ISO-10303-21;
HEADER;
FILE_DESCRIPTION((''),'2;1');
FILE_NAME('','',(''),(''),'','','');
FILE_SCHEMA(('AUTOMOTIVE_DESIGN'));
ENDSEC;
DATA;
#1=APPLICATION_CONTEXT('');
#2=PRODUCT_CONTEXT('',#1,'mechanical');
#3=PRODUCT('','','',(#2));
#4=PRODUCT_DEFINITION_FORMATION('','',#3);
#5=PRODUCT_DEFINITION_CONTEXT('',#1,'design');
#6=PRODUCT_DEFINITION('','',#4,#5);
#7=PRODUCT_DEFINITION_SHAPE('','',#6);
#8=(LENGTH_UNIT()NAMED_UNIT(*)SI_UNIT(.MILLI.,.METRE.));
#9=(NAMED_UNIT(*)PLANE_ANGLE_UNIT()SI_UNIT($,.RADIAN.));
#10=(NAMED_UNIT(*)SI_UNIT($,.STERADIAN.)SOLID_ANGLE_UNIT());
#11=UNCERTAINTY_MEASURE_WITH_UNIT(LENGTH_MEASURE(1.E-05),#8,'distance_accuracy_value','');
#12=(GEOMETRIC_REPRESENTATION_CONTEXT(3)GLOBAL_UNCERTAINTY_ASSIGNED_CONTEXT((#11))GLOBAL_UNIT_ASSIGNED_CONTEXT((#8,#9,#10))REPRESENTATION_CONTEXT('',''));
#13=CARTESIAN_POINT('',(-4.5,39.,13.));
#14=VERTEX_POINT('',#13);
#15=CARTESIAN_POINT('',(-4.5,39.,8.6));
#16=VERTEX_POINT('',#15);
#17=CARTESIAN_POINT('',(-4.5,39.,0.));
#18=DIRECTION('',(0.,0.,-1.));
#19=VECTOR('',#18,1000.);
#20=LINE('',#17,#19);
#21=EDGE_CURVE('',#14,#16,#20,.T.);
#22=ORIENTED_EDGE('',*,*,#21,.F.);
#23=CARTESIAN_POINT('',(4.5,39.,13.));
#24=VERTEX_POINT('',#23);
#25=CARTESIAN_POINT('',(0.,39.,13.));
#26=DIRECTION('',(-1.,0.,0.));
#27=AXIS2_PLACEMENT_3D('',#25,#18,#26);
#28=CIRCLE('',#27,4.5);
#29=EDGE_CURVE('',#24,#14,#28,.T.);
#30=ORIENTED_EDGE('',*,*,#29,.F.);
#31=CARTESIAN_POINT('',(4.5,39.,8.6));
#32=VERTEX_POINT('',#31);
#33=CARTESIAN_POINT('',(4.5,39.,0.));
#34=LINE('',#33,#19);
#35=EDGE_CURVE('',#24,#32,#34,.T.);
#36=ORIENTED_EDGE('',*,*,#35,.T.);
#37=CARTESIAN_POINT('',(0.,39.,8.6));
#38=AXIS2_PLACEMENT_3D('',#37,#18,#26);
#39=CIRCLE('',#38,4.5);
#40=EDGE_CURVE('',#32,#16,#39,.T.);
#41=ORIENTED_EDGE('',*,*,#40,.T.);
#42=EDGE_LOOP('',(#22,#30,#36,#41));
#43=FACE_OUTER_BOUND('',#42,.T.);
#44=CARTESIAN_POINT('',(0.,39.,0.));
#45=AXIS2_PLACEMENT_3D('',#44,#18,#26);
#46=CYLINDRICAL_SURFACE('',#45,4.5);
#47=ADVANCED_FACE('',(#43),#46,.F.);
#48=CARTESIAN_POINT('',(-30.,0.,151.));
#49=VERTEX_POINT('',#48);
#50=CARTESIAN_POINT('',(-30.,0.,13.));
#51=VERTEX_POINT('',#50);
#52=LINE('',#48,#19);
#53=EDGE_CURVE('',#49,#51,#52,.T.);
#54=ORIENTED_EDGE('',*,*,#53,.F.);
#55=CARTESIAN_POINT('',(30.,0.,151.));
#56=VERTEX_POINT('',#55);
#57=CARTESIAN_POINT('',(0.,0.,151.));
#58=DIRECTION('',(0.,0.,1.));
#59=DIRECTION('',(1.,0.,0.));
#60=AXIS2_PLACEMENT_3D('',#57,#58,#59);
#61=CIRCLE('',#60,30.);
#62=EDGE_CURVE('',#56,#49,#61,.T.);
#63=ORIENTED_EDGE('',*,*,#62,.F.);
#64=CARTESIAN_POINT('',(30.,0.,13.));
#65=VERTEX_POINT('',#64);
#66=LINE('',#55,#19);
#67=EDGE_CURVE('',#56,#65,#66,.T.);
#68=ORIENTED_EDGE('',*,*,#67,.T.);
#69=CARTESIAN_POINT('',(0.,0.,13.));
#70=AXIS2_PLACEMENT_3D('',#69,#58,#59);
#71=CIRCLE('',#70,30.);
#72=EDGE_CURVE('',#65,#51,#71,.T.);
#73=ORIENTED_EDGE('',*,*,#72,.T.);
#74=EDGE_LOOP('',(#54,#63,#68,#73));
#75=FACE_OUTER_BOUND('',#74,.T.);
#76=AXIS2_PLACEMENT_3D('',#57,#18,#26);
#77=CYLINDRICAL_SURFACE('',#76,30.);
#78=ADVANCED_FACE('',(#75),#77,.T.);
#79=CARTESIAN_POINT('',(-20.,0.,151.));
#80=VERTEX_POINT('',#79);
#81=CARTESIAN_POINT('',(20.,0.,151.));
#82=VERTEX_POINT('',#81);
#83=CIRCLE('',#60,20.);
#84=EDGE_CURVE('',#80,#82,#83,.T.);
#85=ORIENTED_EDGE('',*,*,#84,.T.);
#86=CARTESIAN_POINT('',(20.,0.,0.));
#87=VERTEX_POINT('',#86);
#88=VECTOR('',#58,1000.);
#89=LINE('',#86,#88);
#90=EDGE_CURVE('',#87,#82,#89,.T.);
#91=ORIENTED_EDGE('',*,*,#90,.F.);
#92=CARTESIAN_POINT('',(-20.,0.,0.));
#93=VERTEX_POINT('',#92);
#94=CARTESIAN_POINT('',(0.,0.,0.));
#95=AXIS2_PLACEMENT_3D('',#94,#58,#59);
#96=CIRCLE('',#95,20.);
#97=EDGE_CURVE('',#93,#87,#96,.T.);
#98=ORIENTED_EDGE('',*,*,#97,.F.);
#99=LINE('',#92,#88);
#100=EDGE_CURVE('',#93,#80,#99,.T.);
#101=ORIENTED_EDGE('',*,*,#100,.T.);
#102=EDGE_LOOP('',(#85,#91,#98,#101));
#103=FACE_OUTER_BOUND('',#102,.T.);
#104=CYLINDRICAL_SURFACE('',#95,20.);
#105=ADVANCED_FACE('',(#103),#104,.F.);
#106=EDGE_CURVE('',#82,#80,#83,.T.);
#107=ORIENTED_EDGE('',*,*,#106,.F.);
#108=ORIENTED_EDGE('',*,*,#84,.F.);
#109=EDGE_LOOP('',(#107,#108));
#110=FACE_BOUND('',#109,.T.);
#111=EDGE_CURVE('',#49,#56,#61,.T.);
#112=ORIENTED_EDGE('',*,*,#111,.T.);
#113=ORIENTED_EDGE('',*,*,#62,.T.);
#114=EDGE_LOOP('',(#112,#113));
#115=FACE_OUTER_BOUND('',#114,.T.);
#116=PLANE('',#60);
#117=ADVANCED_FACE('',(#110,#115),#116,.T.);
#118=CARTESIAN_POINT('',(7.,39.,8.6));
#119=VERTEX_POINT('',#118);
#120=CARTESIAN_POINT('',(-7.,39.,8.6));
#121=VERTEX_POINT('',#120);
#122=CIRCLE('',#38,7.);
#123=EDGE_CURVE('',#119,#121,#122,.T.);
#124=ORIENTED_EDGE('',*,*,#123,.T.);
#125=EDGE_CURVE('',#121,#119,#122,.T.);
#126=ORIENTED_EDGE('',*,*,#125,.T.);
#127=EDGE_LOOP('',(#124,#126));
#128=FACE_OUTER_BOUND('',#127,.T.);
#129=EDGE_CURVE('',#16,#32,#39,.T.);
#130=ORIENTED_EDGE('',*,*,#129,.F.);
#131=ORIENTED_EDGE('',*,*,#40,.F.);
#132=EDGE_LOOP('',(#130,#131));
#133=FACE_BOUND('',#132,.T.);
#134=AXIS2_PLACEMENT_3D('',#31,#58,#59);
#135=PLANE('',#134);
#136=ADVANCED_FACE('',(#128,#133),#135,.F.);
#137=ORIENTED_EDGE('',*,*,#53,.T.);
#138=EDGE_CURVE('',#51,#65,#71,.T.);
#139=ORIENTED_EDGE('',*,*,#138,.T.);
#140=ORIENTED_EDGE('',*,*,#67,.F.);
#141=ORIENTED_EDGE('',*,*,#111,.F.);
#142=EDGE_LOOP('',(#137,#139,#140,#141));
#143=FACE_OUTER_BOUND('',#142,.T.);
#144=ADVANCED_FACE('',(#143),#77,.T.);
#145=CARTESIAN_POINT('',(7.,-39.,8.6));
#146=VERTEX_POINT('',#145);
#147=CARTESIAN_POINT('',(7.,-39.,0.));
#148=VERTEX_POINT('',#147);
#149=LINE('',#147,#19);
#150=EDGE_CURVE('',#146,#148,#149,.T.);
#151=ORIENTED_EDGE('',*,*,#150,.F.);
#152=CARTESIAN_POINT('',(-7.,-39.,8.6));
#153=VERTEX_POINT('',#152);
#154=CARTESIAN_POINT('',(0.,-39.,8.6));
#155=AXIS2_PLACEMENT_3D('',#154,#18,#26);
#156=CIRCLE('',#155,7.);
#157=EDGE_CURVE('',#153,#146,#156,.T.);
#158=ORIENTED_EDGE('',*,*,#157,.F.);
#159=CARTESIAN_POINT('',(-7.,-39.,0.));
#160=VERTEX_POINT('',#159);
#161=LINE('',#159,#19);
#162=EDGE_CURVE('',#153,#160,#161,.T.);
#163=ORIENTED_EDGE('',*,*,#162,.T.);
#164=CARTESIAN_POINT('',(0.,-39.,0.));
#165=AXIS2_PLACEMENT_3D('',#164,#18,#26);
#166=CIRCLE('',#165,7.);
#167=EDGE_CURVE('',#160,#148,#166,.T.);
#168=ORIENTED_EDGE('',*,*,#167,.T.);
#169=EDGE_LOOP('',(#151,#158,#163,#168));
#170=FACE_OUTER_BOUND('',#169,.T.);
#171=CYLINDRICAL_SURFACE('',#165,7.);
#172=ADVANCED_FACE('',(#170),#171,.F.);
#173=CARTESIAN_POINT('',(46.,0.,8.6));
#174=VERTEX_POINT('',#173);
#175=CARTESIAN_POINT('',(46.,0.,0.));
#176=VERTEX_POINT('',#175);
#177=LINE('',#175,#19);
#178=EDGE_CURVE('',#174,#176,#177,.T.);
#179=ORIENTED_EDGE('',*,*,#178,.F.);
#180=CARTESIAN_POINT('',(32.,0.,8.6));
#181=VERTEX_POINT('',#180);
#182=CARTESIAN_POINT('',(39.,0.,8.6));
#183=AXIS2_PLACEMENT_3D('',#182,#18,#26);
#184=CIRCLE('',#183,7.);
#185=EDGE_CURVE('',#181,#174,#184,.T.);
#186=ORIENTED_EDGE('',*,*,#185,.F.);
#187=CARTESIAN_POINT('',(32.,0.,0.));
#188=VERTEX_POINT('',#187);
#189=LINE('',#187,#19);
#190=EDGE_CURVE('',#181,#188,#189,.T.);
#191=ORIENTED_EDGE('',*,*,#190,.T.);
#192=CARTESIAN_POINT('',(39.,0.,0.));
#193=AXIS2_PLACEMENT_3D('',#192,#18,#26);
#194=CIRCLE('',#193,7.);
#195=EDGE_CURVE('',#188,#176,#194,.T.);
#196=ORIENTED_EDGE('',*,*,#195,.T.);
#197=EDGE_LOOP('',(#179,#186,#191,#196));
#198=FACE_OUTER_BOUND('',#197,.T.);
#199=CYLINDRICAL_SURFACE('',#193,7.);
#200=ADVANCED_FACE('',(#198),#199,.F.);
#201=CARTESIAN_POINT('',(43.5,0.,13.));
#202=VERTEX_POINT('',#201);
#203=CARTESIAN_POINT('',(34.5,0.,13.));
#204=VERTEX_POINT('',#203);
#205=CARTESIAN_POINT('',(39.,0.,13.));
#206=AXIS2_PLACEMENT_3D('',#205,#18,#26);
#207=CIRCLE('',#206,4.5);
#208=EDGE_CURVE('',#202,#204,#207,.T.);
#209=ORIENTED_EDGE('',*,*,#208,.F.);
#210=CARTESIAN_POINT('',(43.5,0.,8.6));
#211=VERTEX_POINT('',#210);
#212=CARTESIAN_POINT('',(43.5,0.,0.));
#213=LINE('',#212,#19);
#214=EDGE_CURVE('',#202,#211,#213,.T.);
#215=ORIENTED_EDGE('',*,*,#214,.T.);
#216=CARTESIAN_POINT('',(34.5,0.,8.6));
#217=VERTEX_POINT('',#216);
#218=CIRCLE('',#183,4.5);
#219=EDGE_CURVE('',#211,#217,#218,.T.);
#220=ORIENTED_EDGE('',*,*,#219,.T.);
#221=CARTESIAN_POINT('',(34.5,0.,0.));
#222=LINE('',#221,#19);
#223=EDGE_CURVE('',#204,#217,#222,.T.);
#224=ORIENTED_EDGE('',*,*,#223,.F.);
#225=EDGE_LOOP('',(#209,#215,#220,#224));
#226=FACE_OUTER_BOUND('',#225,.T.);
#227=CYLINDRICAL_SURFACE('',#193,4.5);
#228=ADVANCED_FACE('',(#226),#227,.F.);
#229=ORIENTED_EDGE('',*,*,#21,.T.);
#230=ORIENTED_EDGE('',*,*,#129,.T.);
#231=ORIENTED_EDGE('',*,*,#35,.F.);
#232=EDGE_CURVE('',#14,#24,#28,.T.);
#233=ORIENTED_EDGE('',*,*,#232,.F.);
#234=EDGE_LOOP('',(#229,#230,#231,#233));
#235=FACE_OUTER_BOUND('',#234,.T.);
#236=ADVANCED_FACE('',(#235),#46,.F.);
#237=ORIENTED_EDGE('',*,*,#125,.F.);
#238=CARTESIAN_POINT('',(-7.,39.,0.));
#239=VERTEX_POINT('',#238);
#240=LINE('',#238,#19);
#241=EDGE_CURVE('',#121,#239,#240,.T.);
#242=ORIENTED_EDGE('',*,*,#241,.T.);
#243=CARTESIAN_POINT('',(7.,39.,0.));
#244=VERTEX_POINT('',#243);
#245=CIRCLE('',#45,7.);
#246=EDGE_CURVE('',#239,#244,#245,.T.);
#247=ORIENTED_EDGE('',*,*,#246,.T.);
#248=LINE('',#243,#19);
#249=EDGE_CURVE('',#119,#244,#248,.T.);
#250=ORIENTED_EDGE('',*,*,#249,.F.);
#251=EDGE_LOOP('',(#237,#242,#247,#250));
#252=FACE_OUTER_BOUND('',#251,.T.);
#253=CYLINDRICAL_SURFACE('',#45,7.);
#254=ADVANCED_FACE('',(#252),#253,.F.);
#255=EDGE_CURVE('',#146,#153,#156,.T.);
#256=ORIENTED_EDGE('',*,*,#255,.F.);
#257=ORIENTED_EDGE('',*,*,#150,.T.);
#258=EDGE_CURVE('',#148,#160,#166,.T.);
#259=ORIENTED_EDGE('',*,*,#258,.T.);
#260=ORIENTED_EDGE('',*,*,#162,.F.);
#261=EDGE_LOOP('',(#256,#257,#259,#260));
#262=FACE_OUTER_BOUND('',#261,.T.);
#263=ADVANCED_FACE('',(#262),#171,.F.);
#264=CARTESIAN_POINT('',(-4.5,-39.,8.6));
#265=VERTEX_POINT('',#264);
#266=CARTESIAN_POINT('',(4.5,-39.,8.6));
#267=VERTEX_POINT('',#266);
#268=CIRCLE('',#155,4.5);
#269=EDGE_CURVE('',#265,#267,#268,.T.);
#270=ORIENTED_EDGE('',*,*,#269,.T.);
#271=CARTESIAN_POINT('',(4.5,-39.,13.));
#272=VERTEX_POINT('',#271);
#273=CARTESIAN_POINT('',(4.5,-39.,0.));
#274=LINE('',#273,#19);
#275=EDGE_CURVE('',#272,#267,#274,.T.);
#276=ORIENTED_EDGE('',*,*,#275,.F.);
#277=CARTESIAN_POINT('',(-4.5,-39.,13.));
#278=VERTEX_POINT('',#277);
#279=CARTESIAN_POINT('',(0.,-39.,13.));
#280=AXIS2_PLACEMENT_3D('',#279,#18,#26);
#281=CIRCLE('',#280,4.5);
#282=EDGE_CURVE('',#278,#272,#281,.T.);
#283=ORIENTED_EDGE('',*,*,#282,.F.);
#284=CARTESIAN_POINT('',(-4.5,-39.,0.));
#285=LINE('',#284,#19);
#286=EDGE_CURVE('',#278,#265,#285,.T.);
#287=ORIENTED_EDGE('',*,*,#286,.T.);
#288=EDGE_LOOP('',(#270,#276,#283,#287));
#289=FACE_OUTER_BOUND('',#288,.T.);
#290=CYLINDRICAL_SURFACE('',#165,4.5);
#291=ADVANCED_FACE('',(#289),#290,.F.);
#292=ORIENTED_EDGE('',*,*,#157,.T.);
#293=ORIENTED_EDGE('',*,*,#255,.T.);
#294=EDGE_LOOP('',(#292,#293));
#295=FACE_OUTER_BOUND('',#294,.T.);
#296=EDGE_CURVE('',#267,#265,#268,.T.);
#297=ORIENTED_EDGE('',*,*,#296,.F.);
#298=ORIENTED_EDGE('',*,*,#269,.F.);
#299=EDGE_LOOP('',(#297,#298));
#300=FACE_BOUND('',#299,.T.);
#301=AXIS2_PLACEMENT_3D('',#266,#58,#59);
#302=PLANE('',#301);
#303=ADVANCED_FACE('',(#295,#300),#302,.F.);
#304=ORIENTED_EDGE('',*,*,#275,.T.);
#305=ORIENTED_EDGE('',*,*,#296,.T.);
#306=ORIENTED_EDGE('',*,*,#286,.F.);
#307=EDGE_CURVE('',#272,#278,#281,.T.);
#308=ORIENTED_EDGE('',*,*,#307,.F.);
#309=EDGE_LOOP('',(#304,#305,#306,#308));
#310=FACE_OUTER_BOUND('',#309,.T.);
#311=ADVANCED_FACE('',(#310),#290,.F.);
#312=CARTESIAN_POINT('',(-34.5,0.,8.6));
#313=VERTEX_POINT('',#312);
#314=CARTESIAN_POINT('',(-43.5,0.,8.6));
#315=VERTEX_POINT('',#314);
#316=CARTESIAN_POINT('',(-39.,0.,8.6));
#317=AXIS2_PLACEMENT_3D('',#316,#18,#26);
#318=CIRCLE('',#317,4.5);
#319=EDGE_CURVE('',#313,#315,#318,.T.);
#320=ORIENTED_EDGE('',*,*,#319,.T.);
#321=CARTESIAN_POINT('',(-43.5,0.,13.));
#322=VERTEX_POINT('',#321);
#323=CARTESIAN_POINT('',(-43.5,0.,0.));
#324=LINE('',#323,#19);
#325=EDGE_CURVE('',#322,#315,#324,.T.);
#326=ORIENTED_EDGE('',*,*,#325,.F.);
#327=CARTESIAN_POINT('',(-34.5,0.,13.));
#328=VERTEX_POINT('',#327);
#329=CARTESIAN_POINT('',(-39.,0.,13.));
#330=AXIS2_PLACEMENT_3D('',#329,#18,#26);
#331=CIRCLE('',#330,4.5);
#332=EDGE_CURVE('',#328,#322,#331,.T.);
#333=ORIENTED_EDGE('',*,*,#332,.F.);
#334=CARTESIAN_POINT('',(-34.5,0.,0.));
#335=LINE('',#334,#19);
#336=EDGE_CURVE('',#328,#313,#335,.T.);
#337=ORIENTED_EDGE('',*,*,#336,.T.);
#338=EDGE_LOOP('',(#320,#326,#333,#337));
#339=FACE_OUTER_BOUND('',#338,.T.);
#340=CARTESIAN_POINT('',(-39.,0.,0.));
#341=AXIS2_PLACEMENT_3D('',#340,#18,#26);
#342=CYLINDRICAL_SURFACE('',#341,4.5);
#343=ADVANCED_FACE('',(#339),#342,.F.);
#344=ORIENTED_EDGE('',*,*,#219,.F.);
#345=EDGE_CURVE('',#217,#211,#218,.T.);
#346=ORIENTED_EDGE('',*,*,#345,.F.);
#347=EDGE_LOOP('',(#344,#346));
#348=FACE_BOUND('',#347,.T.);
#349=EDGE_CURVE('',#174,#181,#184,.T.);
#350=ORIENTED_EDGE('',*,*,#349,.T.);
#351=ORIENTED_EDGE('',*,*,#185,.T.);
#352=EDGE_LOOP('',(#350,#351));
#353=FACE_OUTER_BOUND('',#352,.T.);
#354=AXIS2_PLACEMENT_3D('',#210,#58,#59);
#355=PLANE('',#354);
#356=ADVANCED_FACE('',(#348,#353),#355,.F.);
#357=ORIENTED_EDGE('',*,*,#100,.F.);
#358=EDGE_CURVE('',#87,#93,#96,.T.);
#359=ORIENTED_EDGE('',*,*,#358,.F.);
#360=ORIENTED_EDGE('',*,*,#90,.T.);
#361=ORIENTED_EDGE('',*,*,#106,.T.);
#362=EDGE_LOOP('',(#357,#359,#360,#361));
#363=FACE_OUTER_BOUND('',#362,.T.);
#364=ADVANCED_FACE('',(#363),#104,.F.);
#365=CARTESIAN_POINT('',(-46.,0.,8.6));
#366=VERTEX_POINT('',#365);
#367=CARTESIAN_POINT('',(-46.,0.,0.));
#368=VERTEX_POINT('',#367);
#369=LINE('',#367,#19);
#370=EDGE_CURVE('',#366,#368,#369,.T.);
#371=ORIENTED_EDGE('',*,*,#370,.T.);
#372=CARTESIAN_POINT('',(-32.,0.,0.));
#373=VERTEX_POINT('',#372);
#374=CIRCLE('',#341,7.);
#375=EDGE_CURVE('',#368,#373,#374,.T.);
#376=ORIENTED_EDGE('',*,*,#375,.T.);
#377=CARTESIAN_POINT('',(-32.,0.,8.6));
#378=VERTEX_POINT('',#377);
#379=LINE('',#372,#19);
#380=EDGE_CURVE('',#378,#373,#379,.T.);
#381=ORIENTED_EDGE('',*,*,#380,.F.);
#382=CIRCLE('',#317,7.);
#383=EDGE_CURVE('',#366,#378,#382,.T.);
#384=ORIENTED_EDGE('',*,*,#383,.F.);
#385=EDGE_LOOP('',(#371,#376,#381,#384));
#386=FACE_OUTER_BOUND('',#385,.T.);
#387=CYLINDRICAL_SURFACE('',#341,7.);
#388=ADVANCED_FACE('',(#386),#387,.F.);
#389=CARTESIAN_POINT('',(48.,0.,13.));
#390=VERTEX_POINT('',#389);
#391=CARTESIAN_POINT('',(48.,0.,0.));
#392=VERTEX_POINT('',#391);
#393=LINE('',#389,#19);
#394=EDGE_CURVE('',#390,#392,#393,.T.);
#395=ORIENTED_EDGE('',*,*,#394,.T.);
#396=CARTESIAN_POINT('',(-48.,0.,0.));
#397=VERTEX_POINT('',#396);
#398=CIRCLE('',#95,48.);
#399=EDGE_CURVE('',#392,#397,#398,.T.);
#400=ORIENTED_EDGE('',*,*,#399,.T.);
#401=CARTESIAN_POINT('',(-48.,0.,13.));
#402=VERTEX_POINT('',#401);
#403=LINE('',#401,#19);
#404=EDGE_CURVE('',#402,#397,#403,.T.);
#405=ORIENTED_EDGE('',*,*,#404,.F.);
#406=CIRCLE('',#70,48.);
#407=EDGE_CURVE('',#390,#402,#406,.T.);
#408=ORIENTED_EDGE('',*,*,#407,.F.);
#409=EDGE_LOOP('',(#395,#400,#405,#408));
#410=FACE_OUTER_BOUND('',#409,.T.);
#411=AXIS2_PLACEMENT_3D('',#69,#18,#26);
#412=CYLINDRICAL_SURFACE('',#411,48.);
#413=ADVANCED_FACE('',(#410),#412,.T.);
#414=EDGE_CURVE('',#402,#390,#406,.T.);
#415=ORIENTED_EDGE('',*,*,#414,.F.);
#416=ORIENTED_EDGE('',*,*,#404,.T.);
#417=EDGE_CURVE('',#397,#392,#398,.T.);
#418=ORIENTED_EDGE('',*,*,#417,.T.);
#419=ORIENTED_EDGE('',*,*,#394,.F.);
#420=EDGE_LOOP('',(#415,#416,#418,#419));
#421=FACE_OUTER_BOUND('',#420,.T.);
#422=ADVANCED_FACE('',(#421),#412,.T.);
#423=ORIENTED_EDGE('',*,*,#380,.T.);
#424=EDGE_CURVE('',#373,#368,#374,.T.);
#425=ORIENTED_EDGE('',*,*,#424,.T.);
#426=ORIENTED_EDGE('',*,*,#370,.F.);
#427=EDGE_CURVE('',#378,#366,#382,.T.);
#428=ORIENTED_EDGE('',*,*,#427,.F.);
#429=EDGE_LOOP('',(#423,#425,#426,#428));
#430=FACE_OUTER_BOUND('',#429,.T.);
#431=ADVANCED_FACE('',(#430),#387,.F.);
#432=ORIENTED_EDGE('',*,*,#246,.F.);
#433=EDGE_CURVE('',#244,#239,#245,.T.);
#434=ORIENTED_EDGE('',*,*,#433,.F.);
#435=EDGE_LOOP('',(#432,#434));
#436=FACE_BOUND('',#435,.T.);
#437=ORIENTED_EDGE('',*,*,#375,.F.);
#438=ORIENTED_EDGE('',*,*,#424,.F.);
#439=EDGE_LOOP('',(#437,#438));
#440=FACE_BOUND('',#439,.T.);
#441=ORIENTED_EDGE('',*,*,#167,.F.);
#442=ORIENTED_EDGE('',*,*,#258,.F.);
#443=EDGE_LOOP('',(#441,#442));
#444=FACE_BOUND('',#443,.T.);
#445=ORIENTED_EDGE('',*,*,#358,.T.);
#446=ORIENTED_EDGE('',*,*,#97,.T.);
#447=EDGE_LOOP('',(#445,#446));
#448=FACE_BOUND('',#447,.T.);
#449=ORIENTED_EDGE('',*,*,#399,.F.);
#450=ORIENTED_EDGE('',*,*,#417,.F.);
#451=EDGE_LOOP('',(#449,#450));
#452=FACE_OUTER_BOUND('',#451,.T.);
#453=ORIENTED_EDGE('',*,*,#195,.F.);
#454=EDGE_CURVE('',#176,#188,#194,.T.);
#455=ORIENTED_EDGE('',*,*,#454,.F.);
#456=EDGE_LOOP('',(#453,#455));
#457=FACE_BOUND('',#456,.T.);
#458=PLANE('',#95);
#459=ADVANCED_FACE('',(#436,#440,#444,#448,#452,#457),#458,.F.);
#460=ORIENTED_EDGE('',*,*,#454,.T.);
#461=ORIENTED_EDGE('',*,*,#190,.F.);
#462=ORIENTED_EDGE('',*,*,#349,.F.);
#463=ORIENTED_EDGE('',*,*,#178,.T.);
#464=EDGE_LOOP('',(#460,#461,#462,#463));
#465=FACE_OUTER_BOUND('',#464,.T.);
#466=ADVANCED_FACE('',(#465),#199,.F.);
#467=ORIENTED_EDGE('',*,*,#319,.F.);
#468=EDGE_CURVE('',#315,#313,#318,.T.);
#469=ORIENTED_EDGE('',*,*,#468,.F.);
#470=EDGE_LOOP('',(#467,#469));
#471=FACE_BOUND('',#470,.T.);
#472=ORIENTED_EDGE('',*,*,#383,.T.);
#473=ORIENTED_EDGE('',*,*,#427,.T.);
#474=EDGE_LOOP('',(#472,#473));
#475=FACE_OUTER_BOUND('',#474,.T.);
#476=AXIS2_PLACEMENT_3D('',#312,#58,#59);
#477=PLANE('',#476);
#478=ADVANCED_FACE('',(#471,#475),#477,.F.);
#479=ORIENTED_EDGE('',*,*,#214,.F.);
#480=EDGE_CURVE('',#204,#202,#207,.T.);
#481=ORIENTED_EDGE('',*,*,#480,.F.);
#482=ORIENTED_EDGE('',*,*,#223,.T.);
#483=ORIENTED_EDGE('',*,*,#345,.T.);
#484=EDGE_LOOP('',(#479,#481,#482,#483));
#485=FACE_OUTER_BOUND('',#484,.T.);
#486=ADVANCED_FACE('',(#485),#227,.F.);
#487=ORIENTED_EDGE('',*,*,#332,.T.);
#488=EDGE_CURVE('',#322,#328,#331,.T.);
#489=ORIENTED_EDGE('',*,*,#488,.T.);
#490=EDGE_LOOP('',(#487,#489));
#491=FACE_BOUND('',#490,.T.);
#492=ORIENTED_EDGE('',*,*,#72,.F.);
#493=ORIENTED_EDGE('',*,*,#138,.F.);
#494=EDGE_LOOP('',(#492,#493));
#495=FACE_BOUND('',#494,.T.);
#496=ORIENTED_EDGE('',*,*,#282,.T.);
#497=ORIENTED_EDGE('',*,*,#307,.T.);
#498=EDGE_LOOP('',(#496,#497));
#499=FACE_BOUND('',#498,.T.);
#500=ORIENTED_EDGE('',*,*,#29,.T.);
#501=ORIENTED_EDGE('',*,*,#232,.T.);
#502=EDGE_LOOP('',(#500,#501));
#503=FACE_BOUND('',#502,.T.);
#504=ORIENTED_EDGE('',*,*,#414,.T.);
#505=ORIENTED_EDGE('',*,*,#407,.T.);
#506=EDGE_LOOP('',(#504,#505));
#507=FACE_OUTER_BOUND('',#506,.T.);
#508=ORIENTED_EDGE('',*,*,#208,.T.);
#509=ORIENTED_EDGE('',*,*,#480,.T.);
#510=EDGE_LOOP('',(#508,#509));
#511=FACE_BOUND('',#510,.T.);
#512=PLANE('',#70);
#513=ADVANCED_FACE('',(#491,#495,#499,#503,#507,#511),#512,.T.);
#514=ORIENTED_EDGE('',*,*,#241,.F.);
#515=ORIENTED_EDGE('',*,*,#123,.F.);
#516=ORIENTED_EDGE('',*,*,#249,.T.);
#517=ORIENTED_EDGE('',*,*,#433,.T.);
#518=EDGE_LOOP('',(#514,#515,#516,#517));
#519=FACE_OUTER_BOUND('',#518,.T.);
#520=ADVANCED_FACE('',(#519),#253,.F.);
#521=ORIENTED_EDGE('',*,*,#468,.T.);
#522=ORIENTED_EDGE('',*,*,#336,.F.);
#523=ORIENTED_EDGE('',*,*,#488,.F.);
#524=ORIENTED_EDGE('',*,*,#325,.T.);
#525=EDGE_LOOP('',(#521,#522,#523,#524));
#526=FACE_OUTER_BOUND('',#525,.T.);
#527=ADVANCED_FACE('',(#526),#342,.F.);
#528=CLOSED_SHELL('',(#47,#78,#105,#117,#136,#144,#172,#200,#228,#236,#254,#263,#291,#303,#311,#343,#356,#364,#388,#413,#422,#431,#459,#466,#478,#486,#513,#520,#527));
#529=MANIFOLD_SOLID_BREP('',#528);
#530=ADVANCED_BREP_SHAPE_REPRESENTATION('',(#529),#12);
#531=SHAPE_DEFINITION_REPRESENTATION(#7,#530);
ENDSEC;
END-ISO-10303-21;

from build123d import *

# Parameters (mm, degrees)
SKETCH_1_R                   = 48
EXTRUDE_1_DEPTH              = 13
HOLE_WIZARD_M8_1_D           = 9
HOLE_WIZARD_M8_1_CBORE_D     = 14
HOLE_WIZARD_M8_1_CBORE_DEPTH = 8.6
SKETCH_3_R                   = 30
EXTRUDE_2_DEPTH              = 138
SKETCH_4_R                   = 20
CUT_EXTRUDE_3_DEPTH          = 166.556636835


with BuildPart() as part:
    # 草图1 → 拉伸1 (new body)
    with BuildSketch(Plane.XY):
        with Locations(Location((0, 0, 0), (0, 0, 180))):
            Circle(SKETCH_1_R)
    extrude(amount=EXTRUDE_1_DEPTH)

    # M8 六角凹头螺钉的柱形沉头孔1 (through all)
    with Locations(Plane(origin=(0, 39, 0), x_dir=(-1, 0, 0), z_dir=(0, 0, -1))):
        with Locations((0, 0), (-39, -39), (0, -78), (39, -39)):
            CounterBoreHole(HOLE_WIZARD_M8_1_D / 2, HOLE_WIZARD_M8_1_CBORE_D / 2, HOLE_WIZARD_M8_1_CBORE_DEPTH)

    # 草图3 → 拉伸2 (add)
    with BuildSketch(Plane.XY.offset(13)):
        Circle(SKETCH_3_R)
    extrude(amount=EXTRUDE_2_DEPTH)

    # 草图4 → 拉伸3 (cut, through all)
    with BuildSketch(Plane.XY.offset(151)):
        Circle(SKETCH_4_R)
    extrude(amount=-CUT_EXTRUDE_3_DEPTH, mode=Mode.SUBTRACT)


solid = part.part
